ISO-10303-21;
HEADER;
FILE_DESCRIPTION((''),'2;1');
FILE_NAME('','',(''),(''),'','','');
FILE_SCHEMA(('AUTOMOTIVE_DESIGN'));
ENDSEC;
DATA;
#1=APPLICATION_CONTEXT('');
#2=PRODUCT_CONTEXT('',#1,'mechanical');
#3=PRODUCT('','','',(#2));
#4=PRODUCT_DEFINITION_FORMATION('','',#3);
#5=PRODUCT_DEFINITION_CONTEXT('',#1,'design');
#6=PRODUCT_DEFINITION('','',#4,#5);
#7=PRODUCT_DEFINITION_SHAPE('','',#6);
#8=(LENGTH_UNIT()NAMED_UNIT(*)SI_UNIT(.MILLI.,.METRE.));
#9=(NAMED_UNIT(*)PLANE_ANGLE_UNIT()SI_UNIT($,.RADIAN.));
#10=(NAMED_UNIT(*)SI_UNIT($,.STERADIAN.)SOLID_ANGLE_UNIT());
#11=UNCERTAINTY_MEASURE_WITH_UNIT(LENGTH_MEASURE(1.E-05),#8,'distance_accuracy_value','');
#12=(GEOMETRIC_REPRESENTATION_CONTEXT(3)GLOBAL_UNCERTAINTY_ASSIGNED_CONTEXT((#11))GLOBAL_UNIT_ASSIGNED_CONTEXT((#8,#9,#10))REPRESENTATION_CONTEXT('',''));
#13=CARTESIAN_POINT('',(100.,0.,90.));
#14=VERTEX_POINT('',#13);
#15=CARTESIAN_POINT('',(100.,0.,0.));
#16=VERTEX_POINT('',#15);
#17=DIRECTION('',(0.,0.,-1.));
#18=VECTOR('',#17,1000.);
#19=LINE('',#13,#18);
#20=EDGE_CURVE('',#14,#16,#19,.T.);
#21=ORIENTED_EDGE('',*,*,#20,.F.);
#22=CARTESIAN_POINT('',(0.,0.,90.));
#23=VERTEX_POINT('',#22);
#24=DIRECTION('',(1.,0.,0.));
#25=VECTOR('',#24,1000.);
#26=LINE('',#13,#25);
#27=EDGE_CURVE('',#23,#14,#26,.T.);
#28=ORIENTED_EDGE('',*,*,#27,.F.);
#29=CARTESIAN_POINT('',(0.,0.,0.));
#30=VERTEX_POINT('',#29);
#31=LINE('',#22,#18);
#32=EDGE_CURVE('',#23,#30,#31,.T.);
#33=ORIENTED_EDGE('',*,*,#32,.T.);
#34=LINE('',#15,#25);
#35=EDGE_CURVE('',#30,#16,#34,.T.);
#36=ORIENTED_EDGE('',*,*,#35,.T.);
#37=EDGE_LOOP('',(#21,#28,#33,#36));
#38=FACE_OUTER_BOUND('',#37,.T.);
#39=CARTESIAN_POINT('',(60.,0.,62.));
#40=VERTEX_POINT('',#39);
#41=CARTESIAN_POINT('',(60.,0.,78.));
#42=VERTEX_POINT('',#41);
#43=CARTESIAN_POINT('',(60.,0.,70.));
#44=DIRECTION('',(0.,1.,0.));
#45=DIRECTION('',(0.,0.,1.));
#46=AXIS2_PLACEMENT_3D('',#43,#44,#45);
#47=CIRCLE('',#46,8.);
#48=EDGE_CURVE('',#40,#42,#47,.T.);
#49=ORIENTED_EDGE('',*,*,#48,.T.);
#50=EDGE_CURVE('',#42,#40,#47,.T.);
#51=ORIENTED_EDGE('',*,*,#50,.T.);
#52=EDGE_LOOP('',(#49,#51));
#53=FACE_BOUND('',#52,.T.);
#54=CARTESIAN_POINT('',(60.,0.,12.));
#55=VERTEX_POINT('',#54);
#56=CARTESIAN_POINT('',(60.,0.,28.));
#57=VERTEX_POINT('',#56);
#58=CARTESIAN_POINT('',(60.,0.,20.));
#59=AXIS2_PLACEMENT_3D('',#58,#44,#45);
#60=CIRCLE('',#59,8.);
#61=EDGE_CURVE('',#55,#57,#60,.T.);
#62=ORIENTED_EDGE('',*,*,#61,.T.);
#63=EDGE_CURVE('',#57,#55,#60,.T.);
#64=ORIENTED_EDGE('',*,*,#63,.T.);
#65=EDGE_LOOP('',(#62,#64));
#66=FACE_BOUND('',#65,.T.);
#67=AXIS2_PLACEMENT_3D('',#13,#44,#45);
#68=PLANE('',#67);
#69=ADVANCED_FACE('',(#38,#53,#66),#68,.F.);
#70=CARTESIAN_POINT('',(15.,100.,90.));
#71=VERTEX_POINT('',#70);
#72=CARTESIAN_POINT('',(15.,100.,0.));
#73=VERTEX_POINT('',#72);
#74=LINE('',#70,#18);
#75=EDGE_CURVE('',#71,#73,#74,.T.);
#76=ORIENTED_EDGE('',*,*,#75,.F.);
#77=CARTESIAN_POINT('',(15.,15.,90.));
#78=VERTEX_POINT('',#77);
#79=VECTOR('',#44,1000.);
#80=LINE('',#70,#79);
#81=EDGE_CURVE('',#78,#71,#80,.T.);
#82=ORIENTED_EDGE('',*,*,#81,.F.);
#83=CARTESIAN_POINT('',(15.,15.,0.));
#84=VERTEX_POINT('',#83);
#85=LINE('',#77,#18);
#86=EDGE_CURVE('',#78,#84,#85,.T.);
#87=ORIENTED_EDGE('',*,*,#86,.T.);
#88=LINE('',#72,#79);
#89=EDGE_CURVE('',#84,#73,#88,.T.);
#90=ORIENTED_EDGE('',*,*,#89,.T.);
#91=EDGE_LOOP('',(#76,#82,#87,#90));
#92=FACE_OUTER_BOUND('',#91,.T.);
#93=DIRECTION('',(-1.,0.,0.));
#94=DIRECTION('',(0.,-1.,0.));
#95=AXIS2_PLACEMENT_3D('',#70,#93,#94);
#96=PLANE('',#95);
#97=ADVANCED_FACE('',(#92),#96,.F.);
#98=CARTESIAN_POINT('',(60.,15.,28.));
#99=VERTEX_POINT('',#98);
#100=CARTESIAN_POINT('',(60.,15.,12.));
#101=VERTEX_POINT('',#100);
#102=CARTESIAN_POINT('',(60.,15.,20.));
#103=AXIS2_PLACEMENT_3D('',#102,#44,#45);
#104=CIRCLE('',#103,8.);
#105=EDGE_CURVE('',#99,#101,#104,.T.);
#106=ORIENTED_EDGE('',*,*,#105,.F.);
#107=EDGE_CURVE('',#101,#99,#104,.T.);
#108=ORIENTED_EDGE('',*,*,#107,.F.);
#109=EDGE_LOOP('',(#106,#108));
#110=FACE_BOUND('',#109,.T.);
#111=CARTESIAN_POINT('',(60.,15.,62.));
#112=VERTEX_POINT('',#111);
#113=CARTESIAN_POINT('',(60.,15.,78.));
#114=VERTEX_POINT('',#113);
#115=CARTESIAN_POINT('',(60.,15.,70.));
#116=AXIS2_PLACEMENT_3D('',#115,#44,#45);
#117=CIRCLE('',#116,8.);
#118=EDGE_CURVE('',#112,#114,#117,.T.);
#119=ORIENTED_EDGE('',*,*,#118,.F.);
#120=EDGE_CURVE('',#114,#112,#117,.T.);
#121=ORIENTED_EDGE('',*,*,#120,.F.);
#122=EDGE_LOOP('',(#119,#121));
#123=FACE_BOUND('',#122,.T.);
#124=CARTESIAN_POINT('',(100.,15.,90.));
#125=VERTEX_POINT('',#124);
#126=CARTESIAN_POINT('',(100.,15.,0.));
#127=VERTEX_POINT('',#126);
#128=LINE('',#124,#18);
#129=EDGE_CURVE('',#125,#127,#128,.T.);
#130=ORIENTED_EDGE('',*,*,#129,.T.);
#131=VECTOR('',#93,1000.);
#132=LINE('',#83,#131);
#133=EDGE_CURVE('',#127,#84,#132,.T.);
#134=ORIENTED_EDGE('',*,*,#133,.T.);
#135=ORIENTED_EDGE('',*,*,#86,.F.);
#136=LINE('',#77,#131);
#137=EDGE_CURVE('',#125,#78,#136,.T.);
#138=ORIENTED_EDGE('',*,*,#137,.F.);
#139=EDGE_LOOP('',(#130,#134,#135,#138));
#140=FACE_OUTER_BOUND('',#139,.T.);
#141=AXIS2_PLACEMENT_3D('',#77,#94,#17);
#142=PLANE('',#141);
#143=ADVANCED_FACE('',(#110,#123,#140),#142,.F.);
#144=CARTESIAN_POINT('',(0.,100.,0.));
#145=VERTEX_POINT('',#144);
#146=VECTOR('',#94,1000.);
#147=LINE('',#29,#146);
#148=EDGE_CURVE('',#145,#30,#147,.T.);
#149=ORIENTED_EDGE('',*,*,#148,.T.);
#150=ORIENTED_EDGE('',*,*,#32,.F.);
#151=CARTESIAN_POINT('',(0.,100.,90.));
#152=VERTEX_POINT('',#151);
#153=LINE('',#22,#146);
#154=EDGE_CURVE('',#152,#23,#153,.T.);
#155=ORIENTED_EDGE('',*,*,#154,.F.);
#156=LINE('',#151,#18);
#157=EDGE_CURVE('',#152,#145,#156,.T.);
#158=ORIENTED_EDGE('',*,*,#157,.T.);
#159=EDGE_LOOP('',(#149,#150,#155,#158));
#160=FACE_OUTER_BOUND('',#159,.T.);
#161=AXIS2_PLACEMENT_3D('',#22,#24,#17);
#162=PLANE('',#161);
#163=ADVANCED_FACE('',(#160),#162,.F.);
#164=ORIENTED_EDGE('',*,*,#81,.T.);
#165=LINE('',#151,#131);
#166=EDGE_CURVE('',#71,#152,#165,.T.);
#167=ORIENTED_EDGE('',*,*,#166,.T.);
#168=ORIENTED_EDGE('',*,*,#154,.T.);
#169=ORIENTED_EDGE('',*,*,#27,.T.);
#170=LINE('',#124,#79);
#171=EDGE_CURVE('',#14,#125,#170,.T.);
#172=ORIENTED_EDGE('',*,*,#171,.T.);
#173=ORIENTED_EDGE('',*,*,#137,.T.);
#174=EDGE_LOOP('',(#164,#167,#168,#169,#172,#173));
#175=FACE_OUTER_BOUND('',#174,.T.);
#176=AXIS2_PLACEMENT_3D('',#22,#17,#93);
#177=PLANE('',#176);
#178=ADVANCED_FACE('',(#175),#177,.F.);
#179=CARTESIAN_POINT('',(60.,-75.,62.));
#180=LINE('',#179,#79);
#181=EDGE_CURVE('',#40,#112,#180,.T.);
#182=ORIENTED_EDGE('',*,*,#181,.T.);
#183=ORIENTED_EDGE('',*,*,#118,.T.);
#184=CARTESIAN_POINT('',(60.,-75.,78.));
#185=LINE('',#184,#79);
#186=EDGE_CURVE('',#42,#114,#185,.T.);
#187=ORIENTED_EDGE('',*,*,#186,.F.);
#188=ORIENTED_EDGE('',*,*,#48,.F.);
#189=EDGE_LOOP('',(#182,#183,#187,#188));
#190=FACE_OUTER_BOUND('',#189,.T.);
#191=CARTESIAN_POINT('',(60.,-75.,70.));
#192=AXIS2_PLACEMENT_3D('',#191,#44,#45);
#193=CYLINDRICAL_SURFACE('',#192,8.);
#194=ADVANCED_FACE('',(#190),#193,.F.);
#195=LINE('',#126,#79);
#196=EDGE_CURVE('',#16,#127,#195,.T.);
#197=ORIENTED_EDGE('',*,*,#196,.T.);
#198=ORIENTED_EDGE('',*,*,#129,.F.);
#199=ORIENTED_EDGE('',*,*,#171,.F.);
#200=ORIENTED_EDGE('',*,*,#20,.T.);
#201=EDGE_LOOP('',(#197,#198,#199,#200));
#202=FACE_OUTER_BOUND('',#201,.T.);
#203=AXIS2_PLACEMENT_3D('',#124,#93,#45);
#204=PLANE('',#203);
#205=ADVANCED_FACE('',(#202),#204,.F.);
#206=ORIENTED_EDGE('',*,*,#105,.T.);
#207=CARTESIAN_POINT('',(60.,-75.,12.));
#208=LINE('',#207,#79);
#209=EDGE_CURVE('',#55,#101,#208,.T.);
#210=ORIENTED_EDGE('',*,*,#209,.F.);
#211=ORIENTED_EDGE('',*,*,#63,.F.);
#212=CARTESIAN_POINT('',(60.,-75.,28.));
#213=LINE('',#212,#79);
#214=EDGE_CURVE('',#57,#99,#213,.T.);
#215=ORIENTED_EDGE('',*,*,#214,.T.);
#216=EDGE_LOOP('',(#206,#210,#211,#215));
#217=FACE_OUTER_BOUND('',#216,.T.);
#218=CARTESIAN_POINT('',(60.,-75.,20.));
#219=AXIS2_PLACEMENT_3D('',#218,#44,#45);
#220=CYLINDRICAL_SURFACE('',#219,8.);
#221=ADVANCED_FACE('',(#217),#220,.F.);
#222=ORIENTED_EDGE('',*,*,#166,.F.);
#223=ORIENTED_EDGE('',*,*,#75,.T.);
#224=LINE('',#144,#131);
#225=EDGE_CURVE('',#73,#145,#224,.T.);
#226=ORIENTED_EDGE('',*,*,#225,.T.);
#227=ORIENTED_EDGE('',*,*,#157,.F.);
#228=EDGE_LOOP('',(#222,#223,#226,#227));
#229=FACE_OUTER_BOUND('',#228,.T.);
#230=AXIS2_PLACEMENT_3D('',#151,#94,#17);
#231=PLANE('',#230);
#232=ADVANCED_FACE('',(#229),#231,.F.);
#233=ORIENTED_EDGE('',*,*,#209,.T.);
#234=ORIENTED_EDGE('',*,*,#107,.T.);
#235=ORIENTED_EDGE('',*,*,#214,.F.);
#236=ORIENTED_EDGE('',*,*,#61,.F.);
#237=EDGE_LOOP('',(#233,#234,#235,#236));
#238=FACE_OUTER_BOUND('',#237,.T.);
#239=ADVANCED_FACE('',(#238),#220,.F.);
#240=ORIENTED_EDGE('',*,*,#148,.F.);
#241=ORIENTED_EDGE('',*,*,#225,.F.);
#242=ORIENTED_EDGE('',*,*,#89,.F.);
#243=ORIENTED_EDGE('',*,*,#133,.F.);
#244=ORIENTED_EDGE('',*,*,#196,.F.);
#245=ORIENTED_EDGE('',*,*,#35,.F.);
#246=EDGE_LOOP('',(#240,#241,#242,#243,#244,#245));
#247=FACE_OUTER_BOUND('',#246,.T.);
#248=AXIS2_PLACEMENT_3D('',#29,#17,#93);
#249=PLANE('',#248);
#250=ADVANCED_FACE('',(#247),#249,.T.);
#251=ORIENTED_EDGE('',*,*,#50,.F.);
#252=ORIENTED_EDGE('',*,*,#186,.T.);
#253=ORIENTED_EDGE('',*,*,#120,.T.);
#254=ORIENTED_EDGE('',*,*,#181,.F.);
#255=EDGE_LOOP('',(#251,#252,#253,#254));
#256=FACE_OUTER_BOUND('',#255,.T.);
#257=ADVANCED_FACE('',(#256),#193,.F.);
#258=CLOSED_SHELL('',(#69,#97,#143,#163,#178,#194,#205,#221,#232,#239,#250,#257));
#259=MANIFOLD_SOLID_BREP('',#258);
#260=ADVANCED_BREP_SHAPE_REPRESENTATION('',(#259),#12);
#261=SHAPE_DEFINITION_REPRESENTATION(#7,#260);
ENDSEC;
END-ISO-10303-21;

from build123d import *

# Parameters (mm, degrees)
BOSS_EXTRUDE1_DEPTH = 90
SKETCH2_R           = 8
CUT_EXTRUDE1_DEPTH  = 90


with BuildPart() as part:
    # Sketch1 → Boss-Extrude1 (new body)
    with BuildSketch(Plane.XY):
        Polygon((0, 0), (0, 100), (15, 100), (15, 15), (100, 15), (100, 0), align=None)
    extrude(amount=BOSS_EXTRUDE1_DEPTH)

    # Sketch2 → Cut-Extrude1 (cut)
    with BuildSketch(Plane(origin=(0, 15, 0), x_dir=(1, 0, 0), z_dir=(0, 1, 0))):
        with Locations(Location((60, -20, 0), (0, 0, 270))):
            Circle(SKETCH2_R)
        with Locations(Location((60, -70, 0), (0, 0, 270))):
            Circle(SKETCH2_R)
    extrude(amount=-CUT_EXTRUDE1_DEPTH, mode=Mode.SUBTRACT)


solid = part.part
